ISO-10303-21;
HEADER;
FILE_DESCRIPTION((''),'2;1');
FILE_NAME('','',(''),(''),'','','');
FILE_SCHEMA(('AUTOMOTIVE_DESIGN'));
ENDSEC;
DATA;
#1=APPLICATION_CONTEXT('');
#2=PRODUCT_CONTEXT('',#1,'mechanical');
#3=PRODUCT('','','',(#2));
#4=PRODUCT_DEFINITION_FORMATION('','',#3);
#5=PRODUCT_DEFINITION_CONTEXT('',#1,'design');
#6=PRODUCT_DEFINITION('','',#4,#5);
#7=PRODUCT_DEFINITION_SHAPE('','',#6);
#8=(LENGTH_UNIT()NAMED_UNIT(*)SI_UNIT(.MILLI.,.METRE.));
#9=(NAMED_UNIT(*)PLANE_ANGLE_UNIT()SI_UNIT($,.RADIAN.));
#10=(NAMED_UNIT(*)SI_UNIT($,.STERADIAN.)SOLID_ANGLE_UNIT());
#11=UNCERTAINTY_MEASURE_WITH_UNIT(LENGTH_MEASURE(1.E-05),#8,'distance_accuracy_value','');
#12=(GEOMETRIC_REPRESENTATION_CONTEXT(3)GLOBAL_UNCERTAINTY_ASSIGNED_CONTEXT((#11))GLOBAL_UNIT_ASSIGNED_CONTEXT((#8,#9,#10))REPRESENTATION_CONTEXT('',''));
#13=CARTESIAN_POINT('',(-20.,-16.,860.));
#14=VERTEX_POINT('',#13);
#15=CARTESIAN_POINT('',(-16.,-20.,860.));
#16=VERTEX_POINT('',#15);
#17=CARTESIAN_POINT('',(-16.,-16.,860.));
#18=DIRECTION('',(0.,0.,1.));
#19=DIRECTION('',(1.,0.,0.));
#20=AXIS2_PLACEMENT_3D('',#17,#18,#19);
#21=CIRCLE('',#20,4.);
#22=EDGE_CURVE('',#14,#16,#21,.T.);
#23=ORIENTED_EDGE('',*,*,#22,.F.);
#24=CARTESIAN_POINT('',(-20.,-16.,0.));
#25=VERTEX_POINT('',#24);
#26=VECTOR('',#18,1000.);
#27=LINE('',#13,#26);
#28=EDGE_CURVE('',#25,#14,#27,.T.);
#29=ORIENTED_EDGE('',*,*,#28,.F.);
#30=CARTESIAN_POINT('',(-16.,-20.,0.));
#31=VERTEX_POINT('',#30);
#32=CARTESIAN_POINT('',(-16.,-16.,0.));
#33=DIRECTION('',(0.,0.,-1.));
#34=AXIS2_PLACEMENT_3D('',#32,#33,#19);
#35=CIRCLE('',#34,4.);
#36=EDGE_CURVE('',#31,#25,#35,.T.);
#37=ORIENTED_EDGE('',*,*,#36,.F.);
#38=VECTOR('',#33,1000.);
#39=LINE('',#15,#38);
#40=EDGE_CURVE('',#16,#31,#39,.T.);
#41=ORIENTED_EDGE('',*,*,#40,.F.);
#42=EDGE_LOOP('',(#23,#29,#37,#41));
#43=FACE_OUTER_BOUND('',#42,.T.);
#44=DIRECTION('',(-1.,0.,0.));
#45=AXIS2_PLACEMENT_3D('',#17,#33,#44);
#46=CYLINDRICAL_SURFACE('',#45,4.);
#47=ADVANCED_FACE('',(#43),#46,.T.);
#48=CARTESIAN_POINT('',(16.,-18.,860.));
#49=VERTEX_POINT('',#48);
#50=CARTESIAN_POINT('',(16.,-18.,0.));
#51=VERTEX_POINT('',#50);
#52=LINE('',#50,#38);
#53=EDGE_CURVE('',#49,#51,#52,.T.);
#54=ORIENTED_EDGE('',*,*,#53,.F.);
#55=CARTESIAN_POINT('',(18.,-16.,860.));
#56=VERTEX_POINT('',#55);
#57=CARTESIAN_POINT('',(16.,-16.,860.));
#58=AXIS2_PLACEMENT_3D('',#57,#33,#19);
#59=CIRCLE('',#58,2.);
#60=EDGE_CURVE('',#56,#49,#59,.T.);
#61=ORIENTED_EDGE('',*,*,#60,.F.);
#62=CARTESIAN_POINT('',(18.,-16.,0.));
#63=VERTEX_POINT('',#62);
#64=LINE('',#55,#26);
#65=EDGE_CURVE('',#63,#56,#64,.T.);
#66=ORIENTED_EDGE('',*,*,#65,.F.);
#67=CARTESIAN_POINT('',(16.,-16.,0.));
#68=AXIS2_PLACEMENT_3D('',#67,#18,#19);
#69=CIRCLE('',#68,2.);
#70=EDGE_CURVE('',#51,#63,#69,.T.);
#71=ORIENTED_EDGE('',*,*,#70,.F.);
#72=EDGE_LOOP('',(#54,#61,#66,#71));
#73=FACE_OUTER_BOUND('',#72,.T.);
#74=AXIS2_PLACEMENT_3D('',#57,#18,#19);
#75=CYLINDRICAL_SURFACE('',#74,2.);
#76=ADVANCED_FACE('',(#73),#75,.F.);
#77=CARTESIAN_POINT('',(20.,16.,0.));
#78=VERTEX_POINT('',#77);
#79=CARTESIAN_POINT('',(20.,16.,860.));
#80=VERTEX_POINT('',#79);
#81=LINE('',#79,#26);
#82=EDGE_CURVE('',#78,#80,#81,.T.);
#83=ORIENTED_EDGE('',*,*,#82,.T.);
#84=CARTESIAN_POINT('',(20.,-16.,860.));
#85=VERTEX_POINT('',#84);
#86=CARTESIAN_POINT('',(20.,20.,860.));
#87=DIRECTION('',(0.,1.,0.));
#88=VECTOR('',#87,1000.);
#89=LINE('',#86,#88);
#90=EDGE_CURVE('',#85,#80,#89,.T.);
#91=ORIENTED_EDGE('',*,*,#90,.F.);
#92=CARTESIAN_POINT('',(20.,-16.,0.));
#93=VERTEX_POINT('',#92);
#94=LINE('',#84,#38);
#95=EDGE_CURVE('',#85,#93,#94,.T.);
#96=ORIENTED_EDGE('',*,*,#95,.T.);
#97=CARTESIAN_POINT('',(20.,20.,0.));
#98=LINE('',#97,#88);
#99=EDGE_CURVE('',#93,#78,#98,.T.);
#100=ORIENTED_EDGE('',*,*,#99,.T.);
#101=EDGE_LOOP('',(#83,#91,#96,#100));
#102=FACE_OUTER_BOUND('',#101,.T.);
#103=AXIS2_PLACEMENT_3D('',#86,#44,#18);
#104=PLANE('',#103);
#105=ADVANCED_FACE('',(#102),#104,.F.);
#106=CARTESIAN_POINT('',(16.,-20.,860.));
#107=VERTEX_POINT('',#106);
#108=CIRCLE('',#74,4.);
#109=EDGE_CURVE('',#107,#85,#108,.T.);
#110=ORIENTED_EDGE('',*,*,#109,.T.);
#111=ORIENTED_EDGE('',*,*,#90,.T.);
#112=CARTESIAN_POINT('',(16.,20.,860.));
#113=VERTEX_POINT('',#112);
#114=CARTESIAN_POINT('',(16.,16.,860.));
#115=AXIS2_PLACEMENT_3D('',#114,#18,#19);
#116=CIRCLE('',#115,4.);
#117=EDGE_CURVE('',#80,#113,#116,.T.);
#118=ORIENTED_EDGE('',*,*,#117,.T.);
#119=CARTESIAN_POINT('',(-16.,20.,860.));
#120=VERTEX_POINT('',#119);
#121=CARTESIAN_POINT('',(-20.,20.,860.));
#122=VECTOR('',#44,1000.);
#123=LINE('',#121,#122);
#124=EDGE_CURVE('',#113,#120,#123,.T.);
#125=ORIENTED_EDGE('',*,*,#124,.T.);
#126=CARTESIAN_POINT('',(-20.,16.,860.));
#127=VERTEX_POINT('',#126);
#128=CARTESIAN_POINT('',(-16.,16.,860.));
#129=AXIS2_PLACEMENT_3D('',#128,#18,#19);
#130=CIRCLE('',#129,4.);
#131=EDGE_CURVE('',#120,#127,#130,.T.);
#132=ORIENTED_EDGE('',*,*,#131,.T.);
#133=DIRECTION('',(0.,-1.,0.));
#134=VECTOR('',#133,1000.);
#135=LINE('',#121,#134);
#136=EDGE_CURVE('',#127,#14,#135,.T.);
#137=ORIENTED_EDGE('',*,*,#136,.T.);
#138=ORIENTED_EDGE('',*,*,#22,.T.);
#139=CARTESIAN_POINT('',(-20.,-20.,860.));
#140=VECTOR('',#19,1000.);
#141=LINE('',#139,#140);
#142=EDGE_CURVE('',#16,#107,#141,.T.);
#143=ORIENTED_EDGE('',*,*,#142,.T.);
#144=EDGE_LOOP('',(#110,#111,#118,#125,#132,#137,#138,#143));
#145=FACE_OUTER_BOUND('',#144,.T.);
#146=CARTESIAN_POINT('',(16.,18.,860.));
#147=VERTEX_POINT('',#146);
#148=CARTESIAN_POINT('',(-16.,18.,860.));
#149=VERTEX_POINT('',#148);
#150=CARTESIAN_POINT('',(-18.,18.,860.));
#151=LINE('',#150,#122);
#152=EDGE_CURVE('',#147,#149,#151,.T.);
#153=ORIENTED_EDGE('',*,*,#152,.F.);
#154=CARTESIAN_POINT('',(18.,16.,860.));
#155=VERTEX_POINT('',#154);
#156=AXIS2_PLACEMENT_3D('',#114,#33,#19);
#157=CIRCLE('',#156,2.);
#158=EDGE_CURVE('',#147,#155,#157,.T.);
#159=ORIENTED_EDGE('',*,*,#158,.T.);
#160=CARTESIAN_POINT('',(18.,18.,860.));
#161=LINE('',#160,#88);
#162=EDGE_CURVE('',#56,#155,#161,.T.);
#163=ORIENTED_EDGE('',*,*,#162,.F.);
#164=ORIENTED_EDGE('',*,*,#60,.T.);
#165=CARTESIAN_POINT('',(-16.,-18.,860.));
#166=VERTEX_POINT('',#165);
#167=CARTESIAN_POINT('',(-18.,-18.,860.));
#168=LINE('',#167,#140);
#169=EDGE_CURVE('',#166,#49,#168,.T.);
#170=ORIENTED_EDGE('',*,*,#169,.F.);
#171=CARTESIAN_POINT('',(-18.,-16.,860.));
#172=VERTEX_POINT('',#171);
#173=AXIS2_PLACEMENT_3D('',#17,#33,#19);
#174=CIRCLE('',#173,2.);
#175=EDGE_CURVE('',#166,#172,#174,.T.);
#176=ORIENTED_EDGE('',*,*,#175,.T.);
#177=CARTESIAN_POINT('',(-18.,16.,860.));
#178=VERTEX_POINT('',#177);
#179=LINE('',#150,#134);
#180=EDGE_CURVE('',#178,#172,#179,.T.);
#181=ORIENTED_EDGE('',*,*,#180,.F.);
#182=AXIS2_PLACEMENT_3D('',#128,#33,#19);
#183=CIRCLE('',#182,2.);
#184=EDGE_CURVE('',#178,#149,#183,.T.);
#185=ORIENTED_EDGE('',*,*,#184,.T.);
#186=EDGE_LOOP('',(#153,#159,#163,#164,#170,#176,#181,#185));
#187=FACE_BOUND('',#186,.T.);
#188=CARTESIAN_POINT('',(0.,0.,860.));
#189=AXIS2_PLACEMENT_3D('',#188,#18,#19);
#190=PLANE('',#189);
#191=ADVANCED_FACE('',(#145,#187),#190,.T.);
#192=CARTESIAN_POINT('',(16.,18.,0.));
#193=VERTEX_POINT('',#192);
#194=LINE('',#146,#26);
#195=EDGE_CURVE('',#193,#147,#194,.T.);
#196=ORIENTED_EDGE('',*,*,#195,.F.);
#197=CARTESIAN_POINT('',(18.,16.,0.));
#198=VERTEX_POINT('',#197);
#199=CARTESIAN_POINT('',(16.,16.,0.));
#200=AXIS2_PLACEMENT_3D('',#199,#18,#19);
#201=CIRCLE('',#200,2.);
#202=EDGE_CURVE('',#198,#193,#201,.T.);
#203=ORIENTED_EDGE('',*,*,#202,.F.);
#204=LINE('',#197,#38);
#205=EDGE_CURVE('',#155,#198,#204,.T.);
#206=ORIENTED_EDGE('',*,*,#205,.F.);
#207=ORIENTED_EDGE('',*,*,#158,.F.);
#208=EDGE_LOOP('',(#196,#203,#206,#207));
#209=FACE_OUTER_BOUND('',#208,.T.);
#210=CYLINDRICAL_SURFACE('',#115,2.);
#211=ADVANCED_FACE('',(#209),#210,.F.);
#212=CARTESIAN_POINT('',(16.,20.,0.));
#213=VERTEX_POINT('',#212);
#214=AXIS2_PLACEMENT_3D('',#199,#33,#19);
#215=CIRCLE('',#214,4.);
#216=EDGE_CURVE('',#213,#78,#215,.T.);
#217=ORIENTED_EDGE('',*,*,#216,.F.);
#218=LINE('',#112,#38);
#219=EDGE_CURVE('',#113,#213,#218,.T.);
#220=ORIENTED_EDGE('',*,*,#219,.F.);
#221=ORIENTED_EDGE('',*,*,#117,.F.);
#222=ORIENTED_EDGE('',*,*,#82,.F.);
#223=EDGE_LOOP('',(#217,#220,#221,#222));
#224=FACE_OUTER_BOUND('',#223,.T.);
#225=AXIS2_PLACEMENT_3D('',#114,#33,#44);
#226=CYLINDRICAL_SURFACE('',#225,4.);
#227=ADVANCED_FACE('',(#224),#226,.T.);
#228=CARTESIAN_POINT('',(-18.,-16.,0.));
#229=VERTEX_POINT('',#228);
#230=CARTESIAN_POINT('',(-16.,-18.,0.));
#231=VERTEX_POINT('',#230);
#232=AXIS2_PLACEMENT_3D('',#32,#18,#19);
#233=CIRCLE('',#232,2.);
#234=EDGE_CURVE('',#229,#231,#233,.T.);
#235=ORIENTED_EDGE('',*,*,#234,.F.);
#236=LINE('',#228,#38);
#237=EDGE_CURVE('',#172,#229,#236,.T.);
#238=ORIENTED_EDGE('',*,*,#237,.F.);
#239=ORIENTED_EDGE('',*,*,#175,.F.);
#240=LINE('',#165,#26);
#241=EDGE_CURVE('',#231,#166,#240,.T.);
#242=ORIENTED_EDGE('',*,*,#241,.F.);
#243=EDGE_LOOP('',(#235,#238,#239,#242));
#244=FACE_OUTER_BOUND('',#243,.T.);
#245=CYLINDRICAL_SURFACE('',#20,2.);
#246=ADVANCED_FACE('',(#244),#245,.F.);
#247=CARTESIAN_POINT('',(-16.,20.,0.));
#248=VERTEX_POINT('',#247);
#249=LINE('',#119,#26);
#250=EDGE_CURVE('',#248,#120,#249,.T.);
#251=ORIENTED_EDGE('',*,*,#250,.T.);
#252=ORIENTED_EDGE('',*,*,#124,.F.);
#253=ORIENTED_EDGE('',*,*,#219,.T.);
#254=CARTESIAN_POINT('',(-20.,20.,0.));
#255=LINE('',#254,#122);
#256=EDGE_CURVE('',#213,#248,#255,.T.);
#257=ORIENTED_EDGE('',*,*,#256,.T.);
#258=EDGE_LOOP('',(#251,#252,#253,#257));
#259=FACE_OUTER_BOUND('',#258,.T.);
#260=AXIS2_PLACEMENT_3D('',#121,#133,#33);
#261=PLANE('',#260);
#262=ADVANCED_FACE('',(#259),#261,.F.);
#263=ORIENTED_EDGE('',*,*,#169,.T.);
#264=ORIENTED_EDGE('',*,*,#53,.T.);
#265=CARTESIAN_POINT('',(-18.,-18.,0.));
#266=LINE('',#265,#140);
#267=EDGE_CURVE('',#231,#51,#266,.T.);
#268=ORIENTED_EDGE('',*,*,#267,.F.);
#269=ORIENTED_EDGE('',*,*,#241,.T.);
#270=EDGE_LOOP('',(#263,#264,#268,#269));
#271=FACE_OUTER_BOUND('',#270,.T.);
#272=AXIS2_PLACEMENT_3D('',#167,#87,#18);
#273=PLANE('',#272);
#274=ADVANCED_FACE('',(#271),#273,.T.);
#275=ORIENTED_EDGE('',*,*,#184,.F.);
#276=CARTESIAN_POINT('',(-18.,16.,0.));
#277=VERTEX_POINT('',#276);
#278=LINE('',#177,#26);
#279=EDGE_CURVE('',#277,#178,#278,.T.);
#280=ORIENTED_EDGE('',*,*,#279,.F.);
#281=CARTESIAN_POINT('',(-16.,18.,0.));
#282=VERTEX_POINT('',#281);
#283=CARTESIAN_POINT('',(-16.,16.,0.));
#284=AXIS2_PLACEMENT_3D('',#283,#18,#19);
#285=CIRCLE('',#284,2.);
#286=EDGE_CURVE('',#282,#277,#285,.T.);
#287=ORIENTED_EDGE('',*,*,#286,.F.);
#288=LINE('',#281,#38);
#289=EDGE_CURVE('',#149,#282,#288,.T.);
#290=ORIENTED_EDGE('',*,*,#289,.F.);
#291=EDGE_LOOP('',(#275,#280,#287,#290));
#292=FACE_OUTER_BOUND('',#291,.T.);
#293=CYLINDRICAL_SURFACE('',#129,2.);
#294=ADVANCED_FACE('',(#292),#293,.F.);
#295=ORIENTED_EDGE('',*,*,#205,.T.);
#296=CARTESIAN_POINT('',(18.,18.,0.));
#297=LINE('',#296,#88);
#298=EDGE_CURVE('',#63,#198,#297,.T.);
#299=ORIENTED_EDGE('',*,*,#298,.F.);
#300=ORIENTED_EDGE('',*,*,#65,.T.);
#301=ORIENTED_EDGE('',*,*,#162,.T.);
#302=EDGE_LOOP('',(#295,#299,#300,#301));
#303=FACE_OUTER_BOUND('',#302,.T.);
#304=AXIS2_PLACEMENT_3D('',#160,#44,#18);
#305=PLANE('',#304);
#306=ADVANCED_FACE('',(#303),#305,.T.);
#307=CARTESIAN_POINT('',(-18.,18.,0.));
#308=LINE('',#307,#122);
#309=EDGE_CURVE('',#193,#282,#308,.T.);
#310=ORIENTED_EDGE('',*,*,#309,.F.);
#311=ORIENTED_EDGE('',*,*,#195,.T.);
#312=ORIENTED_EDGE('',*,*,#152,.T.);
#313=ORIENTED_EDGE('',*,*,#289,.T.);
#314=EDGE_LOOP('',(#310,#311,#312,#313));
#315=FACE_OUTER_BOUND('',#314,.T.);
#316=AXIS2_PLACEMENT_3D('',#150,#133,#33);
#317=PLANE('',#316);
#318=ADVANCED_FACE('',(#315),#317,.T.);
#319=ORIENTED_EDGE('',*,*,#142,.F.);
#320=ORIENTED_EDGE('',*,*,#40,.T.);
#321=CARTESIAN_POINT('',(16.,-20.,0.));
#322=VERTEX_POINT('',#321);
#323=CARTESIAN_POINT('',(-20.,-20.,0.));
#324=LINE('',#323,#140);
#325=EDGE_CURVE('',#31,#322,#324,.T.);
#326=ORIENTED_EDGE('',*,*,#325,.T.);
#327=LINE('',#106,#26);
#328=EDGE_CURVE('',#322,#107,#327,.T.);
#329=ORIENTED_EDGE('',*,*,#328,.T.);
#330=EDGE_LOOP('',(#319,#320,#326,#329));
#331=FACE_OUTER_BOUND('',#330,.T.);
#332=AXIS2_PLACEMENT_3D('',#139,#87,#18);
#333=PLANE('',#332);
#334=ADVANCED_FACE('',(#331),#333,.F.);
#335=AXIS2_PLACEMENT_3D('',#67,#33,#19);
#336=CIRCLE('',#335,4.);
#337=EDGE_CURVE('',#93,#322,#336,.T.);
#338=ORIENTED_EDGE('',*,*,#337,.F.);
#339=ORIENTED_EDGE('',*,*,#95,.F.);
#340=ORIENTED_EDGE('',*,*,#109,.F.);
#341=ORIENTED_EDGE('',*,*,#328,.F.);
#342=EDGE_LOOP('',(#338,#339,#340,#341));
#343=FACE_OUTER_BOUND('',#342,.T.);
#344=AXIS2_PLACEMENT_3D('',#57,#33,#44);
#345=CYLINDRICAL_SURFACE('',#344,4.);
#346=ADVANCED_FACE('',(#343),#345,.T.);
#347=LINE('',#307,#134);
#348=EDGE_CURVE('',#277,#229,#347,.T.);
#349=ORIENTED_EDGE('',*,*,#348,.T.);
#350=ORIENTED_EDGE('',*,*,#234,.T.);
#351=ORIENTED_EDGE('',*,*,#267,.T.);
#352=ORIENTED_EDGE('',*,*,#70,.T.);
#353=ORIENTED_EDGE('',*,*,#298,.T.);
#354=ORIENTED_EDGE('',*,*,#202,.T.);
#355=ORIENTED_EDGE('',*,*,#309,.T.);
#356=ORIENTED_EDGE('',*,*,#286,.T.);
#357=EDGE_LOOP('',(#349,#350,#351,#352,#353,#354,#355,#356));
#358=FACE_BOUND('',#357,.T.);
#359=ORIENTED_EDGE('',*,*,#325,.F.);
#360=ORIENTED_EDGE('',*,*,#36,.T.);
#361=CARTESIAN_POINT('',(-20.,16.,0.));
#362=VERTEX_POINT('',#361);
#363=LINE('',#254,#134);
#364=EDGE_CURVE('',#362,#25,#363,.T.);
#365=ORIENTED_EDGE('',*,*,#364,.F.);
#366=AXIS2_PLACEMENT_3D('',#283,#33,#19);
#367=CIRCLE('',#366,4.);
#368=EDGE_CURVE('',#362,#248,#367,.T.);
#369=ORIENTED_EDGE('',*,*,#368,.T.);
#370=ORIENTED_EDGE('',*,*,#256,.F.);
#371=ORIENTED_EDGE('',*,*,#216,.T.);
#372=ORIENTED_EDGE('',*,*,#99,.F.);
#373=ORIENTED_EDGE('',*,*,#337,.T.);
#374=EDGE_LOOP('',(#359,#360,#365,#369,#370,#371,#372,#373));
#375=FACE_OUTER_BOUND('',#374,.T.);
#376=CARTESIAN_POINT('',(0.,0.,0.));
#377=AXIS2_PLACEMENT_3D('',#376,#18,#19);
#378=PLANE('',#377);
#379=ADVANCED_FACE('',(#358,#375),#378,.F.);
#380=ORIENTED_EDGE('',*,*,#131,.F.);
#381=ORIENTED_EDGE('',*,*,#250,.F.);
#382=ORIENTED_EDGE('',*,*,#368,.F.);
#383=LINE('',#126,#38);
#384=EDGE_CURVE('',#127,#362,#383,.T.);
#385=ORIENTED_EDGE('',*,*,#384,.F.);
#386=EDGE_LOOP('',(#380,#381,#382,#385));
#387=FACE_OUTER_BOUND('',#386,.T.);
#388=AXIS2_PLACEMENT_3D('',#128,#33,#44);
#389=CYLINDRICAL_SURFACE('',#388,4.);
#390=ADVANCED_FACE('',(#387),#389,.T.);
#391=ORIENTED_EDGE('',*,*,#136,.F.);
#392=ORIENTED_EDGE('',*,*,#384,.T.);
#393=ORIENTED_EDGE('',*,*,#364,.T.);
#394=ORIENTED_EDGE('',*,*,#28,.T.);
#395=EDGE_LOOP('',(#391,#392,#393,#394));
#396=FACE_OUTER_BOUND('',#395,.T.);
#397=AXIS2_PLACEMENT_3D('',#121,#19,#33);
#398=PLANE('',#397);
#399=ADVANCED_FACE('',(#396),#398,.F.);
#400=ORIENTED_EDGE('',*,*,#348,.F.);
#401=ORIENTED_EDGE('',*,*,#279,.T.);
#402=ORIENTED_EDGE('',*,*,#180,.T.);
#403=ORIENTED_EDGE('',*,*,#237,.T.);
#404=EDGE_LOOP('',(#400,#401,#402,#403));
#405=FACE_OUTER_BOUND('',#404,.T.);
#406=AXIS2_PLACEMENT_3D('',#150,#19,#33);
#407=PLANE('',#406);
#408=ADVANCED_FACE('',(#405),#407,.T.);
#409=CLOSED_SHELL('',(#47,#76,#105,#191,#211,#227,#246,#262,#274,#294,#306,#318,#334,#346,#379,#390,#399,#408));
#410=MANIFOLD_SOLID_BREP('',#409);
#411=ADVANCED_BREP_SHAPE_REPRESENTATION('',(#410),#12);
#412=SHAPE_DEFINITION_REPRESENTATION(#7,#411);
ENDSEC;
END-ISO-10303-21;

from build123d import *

# Parameters (mm, degrees)
SKETCH1_W           = 40
SKETCH1_H           = 40
SKETCH1_W_2         = 36
SKETCH1_H_2         = 36
BOSS_EXTRUDE1_DEPTH = 860
FILLET1_R           = 2
FILLET2_R           = 4


with BuildPart() as part:
    # Sketch1 → Boss-Extrude1 (new body)
    with BuildSketch(Plane.XY):
        Rectangle(SKETCH1_W, SKETCH1_H)
        Rectangle(SKETCH1_W_2, SKETCH1_H_2, mode=Mode.SUBTRACT)
    extrude(amount=BOSS_EXTRUDE1_DEPTH)

    # Fillet1
    fillet1_edges = [part.edges().sort_by_distance(p)[0] for p in [
        (18, -18, 430),
        (18, 18, 430),
        (-18, 18, 430),
        (-18, -18, 430),
    ]]
    fillet(fillet1_edges, radius=FILLET1_R)

    # Fillet2
    fillet2_edges = [part.edges().sort_by_distance(p)[0] for p in [
        (20, -20, 430),
        (-20, -20, 430),
        (-20, 20, 430),
        (20, 20, 430),
    ]]
    fillet(fillet2_edges, radius=FILLET2_R)


solid = part.part
